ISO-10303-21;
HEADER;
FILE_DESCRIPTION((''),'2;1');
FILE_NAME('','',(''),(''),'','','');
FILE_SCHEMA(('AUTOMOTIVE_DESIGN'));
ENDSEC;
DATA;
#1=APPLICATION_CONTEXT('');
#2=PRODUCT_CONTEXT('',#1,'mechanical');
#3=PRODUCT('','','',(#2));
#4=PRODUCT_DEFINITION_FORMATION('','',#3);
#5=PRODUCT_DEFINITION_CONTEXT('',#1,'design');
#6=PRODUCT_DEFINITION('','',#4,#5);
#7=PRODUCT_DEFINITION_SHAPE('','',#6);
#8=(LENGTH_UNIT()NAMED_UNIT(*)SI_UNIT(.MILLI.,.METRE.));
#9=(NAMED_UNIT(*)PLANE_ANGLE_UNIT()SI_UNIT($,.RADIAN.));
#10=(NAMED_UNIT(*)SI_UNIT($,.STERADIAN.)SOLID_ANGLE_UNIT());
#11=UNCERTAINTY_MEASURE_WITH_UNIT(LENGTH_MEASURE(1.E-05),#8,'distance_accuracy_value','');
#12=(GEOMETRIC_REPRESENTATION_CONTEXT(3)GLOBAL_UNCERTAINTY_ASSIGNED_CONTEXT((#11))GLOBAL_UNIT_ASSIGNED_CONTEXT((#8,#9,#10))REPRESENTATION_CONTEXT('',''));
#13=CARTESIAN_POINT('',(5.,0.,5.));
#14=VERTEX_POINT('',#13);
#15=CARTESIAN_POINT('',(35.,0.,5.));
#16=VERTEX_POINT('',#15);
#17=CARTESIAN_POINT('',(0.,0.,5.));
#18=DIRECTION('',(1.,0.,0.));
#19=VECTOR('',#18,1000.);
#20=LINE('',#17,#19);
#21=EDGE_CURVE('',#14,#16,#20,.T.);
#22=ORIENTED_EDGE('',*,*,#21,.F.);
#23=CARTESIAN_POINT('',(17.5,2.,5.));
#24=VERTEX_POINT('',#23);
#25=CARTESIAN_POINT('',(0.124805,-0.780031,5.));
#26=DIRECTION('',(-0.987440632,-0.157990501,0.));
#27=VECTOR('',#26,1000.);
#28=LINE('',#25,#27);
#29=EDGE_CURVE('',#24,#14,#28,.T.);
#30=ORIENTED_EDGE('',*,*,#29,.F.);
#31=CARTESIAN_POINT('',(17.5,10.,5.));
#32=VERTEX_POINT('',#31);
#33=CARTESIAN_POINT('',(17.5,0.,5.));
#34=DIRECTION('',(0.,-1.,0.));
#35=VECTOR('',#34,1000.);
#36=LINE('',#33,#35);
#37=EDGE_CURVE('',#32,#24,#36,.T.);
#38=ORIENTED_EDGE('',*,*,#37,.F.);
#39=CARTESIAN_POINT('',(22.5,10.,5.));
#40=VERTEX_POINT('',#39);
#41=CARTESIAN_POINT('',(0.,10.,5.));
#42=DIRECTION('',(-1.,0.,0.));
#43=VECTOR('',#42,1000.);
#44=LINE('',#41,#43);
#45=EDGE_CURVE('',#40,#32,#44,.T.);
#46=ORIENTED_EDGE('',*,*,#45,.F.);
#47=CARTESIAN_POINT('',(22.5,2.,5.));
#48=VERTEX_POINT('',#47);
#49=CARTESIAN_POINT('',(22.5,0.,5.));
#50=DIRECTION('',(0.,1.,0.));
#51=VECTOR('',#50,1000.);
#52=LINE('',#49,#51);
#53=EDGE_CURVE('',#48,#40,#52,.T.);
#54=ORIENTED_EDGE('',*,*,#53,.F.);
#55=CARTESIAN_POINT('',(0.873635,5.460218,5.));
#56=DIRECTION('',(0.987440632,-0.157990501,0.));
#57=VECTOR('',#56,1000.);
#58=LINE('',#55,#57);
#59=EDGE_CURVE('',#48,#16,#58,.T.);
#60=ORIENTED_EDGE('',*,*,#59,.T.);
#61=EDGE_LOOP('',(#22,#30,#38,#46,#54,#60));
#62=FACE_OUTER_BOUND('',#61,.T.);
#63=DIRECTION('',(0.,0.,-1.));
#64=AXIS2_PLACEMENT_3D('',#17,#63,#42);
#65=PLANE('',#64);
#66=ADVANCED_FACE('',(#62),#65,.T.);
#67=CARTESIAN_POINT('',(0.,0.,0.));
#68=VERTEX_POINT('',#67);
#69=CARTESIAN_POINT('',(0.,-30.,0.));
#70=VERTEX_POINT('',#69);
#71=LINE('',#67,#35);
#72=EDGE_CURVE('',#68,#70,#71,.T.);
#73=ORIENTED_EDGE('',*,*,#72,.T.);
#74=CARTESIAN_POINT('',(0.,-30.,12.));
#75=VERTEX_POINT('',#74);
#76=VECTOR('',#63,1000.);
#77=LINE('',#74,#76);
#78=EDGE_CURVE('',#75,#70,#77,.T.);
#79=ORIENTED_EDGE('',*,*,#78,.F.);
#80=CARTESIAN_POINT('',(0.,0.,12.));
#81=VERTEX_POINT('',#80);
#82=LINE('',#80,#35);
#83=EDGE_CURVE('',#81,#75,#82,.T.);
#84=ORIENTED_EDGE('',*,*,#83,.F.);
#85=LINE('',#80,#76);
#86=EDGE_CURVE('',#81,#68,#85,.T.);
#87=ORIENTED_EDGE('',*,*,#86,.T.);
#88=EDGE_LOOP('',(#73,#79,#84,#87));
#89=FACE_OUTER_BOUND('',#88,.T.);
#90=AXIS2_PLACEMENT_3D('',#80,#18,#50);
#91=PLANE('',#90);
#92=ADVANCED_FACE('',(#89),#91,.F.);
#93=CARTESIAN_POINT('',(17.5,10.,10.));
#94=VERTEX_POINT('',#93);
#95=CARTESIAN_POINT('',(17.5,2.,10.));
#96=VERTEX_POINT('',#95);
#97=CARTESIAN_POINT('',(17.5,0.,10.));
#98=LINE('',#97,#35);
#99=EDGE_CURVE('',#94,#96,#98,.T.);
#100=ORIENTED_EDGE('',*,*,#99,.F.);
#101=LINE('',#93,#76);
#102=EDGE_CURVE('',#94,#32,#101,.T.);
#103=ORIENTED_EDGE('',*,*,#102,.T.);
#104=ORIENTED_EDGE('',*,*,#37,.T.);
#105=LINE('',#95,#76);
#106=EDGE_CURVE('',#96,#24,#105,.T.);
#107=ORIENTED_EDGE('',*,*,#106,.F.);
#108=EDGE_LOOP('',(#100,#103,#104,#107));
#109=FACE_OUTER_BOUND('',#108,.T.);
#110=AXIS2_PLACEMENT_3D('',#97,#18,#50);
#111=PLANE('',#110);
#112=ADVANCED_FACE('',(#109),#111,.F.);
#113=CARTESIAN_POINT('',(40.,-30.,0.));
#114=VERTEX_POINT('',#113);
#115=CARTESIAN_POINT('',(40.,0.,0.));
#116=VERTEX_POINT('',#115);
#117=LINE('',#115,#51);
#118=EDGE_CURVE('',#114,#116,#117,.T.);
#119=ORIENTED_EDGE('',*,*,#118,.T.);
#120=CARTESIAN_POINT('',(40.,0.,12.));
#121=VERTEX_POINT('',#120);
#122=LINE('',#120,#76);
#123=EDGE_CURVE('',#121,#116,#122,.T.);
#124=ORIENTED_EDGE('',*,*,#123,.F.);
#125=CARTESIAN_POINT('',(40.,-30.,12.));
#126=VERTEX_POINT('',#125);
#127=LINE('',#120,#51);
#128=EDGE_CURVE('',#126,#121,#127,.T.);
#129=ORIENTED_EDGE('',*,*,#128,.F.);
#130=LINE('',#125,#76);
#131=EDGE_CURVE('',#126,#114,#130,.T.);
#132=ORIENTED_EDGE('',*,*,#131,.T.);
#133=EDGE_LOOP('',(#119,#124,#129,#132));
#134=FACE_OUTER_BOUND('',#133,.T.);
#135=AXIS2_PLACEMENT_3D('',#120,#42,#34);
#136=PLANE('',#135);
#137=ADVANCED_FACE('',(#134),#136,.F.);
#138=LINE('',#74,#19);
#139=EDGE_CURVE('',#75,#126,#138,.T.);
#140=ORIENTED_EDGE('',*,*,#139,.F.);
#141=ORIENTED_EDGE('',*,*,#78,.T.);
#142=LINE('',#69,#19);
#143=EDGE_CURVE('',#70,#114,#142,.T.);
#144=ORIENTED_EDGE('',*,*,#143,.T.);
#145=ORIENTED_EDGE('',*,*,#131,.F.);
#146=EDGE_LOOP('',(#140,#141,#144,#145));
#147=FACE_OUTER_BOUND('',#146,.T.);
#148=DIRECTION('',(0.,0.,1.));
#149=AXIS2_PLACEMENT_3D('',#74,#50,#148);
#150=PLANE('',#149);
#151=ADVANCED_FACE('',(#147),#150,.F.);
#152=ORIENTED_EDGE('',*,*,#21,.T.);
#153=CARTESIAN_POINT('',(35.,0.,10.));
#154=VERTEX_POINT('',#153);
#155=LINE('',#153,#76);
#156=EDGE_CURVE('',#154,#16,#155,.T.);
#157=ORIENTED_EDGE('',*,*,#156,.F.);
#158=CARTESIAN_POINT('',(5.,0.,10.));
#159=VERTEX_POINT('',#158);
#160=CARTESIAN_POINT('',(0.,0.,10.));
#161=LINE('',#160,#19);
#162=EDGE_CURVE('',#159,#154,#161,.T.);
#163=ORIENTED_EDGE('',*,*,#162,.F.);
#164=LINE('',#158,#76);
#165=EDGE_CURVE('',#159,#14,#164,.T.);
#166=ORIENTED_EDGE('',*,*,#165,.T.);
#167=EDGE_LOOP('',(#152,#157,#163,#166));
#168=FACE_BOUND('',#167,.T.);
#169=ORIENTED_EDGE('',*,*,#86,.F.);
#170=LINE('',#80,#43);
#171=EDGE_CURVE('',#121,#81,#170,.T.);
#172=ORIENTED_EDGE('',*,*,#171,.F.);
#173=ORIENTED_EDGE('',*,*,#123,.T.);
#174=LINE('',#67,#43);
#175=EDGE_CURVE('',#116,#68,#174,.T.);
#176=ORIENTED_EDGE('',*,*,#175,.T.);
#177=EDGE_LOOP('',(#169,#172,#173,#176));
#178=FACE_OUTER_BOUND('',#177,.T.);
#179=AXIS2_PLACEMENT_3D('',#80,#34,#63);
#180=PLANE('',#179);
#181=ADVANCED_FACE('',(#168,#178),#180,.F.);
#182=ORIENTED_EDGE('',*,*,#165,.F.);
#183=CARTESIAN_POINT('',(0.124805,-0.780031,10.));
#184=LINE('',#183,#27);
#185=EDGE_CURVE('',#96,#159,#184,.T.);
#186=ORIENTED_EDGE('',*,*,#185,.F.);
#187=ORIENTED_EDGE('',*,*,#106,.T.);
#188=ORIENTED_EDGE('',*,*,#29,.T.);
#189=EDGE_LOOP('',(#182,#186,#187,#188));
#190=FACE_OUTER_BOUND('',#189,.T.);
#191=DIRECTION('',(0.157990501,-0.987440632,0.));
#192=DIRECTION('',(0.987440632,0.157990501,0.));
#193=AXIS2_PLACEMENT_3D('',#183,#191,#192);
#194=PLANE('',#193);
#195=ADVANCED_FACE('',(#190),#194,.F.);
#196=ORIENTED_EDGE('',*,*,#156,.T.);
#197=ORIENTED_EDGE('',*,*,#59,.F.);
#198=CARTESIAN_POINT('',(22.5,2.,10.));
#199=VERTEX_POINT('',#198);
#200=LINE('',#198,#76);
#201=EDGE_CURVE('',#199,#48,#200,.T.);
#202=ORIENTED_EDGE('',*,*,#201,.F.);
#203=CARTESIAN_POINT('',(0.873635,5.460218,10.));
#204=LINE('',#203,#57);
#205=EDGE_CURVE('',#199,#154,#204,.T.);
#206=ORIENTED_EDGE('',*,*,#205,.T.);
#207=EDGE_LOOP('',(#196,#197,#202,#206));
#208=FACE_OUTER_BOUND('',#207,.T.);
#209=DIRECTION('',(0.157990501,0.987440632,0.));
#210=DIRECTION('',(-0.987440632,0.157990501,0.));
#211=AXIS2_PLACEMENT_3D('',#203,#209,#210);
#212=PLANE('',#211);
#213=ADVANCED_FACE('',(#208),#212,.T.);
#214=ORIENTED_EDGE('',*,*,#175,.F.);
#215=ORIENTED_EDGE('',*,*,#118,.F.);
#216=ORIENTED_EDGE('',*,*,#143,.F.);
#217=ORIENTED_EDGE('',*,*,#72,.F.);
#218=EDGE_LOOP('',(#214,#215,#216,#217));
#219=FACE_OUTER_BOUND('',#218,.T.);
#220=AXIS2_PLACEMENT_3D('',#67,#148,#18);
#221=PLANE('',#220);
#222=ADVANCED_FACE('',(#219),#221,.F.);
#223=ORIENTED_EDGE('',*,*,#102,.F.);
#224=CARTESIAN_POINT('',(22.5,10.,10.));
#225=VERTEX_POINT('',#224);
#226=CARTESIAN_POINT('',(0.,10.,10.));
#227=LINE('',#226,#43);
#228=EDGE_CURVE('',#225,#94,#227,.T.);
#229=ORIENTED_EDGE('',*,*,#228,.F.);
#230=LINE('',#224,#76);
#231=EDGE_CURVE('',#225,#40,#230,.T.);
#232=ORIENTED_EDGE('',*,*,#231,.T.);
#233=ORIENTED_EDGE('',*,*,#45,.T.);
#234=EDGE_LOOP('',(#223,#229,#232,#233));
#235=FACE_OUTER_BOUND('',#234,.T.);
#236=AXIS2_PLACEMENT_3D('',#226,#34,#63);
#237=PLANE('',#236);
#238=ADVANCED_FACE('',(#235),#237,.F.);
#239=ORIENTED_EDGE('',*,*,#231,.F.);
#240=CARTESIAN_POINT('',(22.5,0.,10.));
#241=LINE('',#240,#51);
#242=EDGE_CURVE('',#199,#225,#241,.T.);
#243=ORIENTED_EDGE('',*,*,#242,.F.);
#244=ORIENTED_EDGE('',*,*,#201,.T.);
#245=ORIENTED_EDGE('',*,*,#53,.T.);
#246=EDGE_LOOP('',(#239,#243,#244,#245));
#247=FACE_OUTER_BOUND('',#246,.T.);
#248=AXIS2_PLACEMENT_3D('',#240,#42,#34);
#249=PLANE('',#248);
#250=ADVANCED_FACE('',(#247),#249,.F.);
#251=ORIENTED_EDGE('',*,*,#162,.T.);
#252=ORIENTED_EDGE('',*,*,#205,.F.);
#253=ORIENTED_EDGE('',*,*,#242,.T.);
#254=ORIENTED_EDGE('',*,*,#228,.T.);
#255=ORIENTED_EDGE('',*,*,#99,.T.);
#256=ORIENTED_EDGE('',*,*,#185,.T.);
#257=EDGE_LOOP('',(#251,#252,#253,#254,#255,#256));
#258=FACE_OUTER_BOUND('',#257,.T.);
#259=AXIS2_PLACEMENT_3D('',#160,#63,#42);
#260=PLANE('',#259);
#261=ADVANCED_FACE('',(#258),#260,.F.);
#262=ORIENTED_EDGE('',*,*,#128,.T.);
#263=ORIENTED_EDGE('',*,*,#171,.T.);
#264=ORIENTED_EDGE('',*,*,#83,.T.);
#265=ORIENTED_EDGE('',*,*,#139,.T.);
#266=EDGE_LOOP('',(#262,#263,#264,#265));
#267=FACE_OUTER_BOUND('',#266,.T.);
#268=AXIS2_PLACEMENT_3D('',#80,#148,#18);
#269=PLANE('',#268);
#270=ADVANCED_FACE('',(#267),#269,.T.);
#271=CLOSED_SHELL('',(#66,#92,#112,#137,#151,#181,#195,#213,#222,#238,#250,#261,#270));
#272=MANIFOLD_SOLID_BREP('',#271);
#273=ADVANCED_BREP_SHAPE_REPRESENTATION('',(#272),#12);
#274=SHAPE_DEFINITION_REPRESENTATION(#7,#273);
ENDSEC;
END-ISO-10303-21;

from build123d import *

# Parameters (mm, degrees)
SKETCH1_W           = 40
SKETCH1_H           = 30
BOSS_EXTRUDE1_DEPTH = 12
BOSS_EXTRUDE3_START = 5
BOSS_EXTRUDE3_DEPTH = 5


with BuildPart() as part:
    # Sketch1 → Boss-Extrude1 (new body)
    with BuildSketch(Plane.XY):
        with Locations((20, -15)):
            Rectangle(SKETCH1_W, SKETCH1_H)
    extrude(amount=BOSS_EXTRUDE1_DEPTH)

    # Sketch2 → Boss-Extrude3 (add)
    with BuildSketch(Plane.XY.offset(BOSS_EXTRUDE3_START)):
        Polygon((17.5, 10), (17.5, 2), (5, 0), (35, 0), (22.5, 2), (22.5, 10), align=None)
    extrude(amount=BOSS_EXTRUDE3_DEPTH)


solid = part.part
